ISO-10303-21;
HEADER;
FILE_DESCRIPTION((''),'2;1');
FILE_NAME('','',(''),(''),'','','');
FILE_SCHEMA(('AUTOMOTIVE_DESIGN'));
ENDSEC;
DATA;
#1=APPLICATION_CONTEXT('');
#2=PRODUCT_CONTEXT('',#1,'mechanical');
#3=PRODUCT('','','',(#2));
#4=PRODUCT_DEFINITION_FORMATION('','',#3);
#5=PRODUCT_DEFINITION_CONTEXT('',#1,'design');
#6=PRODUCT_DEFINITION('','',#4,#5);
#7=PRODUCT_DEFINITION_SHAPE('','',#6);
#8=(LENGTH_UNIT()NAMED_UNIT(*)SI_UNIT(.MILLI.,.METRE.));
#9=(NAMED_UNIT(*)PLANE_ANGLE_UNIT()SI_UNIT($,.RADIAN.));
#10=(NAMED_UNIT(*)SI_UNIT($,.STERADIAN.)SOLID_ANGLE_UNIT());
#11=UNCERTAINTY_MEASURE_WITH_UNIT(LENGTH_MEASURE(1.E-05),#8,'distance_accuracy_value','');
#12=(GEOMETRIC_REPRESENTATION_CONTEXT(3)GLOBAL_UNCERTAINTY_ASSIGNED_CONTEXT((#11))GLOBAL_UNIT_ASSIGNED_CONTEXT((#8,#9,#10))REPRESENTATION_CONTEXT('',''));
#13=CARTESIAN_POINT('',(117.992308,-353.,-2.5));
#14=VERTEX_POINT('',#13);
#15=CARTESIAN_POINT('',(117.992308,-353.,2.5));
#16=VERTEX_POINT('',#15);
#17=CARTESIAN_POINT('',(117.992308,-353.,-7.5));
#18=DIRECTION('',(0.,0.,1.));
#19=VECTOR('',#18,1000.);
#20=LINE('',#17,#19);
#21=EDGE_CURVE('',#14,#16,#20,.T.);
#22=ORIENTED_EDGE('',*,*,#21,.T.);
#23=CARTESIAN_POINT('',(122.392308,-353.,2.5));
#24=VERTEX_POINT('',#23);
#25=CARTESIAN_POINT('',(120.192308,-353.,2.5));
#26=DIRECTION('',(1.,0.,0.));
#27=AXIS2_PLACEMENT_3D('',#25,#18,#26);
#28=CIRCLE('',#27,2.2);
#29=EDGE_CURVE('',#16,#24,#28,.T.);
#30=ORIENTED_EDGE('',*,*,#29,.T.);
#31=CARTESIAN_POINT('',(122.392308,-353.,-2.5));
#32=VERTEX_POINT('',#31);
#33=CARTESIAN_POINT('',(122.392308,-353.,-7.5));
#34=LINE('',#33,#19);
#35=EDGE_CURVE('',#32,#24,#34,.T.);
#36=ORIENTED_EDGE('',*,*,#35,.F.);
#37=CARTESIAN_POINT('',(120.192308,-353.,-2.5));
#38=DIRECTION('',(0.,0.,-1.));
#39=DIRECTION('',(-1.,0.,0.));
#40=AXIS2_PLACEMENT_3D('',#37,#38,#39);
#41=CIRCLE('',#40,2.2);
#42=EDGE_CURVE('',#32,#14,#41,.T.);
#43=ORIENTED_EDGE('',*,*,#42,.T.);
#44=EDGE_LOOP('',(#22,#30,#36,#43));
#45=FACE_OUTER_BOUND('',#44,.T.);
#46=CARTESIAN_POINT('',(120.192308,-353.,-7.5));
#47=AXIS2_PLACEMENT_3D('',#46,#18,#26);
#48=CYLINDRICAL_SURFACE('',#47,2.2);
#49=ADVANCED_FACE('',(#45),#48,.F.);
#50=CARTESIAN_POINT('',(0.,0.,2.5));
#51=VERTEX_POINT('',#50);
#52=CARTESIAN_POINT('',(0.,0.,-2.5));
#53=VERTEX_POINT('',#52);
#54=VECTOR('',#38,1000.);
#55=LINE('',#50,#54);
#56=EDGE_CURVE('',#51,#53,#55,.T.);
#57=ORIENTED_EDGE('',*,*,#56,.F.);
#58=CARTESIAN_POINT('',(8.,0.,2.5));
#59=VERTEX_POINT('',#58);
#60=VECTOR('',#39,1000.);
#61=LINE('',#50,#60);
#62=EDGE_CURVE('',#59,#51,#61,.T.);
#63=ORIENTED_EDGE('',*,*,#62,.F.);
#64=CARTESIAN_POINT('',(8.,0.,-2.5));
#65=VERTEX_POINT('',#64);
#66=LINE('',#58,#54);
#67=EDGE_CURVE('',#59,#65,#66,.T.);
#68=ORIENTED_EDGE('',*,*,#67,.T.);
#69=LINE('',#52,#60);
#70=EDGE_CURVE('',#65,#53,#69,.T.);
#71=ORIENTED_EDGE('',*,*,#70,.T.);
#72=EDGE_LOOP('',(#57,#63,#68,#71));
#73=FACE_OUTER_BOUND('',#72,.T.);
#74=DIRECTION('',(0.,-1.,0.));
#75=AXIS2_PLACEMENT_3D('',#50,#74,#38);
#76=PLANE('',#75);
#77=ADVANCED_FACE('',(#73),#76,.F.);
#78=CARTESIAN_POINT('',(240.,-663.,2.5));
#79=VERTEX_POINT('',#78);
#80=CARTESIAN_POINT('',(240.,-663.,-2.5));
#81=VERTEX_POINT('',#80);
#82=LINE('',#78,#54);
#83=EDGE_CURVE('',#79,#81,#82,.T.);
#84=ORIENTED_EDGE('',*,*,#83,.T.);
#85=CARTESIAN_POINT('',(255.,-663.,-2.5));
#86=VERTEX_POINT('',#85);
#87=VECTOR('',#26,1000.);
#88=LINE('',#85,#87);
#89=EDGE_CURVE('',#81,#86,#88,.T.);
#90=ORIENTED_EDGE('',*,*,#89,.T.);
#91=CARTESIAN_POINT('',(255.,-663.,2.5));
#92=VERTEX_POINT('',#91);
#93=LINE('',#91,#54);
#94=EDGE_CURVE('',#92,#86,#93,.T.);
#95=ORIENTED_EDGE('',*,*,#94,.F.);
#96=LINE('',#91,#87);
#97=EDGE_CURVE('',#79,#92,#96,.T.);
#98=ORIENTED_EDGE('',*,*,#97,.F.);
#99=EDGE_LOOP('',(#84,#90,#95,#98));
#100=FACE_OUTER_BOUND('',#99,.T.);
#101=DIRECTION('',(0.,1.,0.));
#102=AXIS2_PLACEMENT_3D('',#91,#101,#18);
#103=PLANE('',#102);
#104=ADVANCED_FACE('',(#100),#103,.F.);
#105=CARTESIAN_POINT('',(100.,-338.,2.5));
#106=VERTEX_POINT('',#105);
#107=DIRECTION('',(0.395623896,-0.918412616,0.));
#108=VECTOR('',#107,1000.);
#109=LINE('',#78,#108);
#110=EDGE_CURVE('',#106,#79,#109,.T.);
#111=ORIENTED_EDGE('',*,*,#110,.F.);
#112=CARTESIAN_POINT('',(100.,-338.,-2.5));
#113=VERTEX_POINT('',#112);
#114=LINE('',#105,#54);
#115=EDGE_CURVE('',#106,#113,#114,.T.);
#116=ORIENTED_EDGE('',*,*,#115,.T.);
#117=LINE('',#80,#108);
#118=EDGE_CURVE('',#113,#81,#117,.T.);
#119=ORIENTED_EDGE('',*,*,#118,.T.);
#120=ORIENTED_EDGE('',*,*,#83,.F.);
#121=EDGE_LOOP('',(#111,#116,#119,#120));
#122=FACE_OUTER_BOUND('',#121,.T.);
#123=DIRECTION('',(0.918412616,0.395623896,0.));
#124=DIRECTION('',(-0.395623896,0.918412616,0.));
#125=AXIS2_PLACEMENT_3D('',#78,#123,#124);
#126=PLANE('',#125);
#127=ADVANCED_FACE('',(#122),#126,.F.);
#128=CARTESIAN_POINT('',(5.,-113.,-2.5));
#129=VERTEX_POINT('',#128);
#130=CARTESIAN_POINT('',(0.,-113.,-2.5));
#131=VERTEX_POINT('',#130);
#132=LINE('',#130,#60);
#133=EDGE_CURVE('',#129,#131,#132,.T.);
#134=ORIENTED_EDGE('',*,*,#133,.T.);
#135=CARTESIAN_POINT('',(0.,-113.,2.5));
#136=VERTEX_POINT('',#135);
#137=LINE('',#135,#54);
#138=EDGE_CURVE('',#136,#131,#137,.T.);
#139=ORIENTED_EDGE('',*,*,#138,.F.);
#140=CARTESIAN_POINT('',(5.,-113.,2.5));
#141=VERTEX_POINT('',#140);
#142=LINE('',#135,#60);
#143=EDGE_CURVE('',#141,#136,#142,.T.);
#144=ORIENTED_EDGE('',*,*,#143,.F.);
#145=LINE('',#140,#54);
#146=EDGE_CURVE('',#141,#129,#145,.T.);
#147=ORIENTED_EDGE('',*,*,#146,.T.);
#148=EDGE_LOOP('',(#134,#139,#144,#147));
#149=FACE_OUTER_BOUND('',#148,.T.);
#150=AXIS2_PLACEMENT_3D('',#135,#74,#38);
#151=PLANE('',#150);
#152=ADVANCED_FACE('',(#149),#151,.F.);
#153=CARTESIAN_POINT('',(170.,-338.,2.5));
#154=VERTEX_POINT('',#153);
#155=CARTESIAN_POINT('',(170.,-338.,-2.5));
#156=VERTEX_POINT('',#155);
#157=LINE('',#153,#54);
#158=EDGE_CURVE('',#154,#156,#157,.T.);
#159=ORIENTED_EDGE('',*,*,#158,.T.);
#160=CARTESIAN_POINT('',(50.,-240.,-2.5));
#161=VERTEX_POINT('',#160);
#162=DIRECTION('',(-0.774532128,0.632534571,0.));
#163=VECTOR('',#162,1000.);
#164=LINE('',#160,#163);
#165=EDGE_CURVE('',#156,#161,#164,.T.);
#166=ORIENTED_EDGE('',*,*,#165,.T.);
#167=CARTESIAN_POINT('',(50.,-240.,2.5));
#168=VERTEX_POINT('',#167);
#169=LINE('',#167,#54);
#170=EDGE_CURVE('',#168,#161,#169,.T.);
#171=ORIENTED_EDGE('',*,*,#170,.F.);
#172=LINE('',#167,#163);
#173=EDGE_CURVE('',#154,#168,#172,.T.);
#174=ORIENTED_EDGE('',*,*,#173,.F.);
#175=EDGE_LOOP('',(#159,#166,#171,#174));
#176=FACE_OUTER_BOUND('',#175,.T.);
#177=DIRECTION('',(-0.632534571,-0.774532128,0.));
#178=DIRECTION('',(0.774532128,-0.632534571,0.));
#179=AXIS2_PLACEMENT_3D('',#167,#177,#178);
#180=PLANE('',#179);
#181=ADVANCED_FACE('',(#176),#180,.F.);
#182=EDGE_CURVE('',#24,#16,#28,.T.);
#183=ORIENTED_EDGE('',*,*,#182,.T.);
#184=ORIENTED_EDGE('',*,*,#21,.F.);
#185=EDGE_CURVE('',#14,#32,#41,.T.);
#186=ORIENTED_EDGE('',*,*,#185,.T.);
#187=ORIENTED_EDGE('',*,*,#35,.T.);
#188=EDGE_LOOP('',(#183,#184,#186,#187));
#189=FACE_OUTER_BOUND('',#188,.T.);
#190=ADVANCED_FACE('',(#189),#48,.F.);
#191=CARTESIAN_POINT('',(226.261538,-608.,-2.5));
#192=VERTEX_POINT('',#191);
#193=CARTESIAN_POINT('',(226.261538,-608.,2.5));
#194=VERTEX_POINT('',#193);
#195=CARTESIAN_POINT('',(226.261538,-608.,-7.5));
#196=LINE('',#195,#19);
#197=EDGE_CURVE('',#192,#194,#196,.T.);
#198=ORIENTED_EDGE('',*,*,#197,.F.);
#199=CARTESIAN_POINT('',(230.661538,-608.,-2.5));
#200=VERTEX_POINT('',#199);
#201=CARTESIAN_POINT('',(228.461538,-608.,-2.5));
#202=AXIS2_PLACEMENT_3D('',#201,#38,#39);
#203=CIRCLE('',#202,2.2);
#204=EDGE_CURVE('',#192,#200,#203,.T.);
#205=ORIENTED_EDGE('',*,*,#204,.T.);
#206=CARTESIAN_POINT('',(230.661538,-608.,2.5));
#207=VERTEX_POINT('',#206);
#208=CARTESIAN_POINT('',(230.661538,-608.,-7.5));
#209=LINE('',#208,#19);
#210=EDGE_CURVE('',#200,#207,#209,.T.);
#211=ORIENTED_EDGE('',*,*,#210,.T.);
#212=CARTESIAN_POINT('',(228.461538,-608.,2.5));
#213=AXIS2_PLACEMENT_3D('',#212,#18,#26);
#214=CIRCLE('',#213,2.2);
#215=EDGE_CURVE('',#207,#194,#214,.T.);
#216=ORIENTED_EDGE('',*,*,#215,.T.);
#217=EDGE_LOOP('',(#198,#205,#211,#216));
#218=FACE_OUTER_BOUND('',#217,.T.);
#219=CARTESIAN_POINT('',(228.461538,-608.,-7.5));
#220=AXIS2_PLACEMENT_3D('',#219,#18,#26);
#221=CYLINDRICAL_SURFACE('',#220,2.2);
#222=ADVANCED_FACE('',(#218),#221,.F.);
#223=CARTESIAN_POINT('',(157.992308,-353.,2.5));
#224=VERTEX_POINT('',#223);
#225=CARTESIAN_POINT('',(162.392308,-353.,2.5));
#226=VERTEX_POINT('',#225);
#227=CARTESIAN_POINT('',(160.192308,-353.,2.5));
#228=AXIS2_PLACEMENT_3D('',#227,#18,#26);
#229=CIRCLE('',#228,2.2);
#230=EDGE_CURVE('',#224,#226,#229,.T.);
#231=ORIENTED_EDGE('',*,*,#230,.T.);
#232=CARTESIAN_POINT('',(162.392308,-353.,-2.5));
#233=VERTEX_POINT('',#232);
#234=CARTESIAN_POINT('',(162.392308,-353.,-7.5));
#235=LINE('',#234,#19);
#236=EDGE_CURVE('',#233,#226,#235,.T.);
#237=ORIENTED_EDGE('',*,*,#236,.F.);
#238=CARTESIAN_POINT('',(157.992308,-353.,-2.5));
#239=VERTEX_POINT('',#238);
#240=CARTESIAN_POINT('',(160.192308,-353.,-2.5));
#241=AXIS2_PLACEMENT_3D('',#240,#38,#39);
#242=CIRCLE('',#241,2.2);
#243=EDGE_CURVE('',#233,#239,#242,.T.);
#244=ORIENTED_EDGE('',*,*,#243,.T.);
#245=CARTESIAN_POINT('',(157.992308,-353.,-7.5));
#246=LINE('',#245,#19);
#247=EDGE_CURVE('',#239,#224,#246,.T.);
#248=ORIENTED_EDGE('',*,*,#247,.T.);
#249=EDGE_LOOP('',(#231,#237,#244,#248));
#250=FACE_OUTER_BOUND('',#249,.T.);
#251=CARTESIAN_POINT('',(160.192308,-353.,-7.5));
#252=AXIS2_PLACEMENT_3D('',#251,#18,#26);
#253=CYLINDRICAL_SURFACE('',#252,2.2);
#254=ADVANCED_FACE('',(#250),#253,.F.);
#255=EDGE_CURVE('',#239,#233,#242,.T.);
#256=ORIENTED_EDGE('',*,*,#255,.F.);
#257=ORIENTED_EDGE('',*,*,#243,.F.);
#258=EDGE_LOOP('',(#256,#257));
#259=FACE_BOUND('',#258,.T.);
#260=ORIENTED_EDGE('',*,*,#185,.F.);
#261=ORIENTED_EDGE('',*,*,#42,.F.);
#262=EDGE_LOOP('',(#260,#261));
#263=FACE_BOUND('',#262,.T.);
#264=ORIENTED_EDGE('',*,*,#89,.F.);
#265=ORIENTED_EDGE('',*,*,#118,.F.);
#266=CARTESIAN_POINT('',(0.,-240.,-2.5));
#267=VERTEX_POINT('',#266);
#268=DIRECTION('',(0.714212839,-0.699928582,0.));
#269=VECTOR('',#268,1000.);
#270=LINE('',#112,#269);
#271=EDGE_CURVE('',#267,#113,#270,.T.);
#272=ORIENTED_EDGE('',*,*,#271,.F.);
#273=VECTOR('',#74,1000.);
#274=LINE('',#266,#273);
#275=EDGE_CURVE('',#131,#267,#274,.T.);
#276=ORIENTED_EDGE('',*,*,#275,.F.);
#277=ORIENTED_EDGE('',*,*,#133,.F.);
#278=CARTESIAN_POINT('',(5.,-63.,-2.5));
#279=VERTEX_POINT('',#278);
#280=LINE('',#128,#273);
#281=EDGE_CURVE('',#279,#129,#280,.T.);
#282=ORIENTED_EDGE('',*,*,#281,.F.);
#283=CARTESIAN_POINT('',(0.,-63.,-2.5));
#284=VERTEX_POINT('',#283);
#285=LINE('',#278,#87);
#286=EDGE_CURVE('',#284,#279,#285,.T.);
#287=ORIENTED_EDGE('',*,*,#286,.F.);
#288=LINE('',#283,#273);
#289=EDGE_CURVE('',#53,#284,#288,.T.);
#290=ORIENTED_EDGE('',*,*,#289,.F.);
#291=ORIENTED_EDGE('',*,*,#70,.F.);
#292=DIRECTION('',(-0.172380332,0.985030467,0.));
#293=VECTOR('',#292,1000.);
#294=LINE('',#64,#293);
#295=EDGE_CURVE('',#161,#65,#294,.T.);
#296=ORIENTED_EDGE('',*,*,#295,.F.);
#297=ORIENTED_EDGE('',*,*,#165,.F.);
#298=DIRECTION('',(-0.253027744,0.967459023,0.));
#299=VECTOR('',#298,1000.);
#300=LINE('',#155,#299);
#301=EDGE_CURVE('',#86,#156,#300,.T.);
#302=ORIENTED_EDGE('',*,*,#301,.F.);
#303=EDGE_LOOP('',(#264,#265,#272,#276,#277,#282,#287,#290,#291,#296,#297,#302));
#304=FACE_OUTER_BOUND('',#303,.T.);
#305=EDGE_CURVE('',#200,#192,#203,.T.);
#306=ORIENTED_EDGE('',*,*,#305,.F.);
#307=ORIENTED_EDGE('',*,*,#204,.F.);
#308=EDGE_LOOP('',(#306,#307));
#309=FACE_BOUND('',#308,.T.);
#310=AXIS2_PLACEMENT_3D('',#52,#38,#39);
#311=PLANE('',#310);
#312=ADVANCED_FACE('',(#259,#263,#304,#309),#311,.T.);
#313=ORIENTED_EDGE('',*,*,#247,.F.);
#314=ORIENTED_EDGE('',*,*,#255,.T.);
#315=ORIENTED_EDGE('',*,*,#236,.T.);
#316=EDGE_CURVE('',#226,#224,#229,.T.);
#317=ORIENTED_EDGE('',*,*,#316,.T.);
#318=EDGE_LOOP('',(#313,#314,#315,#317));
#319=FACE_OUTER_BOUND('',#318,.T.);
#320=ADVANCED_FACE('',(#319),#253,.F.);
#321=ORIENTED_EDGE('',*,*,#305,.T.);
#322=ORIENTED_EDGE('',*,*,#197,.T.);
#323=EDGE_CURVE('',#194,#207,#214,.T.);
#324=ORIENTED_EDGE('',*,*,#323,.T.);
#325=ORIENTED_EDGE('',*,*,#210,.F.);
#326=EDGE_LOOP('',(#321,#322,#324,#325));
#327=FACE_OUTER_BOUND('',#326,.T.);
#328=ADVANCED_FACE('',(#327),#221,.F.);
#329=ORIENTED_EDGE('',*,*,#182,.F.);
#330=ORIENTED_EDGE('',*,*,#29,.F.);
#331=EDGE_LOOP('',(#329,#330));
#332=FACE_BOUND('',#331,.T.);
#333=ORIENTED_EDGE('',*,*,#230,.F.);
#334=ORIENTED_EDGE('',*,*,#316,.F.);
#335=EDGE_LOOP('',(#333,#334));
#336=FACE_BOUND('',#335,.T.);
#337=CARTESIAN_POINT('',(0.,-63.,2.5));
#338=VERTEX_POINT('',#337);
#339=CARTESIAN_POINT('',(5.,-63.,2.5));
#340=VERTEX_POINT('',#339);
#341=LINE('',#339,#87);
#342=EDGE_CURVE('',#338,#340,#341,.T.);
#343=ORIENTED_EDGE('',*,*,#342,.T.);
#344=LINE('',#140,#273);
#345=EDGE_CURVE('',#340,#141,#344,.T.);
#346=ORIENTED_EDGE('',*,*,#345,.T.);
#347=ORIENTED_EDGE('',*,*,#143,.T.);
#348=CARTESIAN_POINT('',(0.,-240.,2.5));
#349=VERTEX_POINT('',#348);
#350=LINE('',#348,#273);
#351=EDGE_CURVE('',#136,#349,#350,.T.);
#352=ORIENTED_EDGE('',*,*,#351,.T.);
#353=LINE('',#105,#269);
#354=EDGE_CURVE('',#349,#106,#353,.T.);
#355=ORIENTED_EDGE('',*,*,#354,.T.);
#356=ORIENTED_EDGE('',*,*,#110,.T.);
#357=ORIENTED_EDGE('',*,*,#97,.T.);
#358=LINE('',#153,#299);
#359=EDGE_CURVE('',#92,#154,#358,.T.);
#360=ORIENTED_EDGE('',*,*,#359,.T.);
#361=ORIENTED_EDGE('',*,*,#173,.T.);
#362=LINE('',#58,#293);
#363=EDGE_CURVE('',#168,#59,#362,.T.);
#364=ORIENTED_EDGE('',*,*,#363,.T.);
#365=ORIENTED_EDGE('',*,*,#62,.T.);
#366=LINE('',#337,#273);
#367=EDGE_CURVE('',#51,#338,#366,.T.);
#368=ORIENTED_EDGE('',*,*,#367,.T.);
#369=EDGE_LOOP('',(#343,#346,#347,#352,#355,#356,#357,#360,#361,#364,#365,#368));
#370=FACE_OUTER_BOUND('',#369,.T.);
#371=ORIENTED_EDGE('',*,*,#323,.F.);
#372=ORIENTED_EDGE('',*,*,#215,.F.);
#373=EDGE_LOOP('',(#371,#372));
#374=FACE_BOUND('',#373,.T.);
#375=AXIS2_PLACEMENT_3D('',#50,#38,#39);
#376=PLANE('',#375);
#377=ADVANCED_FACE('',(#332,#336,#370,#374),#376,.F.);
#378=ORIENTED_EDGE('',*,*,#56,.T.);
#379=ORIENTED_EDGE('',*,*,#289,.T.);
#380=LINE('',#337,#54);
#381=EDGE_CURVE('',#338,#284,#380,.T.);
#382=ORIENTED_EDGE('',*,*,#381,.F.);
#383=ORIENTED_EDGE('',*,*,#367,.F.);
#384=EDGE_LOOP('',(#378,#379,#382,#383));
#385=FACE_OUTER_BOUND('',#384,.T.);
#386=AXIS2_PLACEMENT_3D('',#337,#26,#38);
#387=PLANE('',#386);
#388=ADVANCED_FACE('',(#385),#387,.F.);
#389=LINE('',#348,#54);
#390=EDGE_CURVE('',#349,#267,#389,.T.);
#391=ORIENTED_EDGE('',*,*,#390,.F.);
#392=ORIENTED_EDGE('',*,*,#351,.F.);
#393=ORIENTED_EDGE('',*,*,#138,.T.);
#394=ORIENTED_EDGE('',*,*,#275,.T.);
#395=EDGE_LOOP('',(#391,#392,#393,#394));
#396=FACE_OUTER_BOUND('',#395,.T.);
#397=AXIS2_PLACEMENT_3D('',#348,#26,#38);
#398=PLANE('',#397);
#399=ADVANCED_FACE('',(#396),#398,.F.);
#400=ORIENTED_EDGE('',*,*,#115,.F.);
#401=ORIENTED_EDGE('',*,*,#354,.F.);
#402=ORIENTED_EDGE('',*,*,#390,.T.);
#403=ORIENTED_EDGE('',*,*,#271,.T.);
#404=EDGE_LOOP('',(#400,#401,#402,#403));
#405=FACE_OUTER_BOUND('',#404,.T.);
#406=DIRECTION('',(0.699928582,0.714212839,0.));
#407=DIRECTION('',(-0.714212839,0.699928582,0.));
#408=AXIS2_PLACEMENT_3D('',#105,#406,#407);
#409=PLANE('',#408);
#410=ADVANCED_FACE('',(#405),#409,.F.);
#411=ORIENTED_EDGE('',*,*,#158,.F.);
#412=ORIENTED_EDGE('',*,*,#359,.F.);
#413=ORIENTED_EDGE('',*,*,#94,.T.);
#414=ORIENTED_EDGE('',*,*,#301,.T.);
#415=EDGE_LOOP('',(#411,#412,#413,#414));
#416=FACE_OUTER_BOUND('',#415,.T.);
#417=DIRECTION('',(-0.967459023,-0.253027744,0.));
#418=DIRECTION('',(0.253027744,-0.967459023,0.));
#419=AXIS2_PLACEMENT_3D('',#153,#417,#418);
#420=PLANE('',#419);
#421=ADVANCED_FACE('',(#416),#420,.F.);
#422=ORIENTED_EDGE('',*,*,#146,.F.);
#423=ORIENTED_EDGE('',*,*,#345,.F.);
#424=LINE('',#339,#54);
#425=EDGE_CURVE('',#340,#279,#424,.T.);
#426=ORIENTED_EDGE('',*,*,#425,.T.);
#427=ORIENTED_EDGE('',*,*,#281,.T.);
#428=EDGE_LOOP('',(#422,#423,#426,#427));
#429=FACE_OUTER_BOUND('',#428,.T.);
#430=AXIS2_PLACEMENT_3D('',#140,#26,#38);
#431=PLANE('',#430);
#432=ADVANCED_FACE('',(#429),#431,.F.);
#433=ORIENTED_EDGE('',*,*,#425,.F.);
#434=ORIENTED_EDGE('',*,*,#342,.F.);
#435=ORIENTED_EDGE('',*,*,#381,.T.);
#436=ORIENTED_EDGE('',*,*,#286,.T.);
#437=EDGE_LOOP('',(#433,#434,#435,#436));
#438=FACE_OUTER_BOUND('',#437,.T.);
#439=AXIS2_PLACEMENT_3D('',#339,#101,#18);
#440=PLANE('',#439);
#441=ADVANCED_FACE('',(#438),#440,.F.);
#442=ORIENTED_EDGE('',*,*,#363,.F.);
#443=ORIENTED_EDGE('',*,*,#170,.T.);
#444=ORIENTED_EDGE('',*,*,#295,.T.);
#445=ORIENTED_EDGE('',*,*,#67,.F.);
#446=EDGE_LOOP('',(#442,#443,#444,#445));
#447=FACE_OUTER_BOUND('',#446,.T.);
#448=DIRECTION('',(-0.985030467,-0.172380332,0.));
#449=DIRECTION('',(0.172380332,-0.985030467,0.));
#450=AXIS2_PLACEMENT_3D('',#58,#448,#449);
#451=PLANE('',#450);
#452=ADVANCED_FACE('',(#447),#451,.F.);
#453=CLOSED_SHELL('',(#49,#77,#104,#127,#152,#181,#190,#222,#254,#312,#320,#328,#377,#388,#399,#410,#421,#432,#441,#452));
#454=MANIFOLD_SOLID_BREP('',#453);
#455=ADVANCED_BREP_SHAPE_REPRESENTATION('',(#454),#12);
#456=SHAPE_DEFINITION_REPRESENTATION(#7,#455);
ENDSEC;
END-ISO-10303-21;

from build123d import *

# Parameters (mm, degrees)
EXTRUDE_1_DEPTH     = 2.5
SKETCH_2_R          = 2.2
CUT_EXTRUDE_1_DEPTH = 10
SKETCH_3_R          = 2.2
CUT_EXTRUDE_2_DEPTH = 10


with BuildPart() as part:
    # 草图1 → 凸台-拉伸1 (new, symmetric)
    with BuildSketch(Plane.XY):
        Polygon((0, 0), (8, 0), (50, -240), (170, -338), (255, -663), (240, -663), (100, -338), (0, -240), (0, -113), (5, -113), (5, -63), (0, -63), align=None)
    extrude(amount=EXTRUDE_1_DEPTH, both=True)

    # 草图2 → 切除-拉伸1 (cut)
    with BuildSketch(Plane.XY.offset(2.5)):
        with Locations((120.192307692, -353)):
            Circle(SKETCH_2_R)
        with Locations((160.192307692, -353)):
            Circle(SKETCH_2_R)
    extrude(amount=-CUT_EXTRUDE_1_DEPTH, mode=Mode.SUBTRACT)

    # 草图3 → 切除-拉伸2 (cut)
    with BuildSketch(Plane.XY.offset(2.5)):
        with Locations((228.461538462, -608)):
            Circle(SKETCH_3_R)
    extrude(amount=-CUT_EXTRUDE_2_DEPTH, mode=Mode.SUBTRACT)


solid = part.part
